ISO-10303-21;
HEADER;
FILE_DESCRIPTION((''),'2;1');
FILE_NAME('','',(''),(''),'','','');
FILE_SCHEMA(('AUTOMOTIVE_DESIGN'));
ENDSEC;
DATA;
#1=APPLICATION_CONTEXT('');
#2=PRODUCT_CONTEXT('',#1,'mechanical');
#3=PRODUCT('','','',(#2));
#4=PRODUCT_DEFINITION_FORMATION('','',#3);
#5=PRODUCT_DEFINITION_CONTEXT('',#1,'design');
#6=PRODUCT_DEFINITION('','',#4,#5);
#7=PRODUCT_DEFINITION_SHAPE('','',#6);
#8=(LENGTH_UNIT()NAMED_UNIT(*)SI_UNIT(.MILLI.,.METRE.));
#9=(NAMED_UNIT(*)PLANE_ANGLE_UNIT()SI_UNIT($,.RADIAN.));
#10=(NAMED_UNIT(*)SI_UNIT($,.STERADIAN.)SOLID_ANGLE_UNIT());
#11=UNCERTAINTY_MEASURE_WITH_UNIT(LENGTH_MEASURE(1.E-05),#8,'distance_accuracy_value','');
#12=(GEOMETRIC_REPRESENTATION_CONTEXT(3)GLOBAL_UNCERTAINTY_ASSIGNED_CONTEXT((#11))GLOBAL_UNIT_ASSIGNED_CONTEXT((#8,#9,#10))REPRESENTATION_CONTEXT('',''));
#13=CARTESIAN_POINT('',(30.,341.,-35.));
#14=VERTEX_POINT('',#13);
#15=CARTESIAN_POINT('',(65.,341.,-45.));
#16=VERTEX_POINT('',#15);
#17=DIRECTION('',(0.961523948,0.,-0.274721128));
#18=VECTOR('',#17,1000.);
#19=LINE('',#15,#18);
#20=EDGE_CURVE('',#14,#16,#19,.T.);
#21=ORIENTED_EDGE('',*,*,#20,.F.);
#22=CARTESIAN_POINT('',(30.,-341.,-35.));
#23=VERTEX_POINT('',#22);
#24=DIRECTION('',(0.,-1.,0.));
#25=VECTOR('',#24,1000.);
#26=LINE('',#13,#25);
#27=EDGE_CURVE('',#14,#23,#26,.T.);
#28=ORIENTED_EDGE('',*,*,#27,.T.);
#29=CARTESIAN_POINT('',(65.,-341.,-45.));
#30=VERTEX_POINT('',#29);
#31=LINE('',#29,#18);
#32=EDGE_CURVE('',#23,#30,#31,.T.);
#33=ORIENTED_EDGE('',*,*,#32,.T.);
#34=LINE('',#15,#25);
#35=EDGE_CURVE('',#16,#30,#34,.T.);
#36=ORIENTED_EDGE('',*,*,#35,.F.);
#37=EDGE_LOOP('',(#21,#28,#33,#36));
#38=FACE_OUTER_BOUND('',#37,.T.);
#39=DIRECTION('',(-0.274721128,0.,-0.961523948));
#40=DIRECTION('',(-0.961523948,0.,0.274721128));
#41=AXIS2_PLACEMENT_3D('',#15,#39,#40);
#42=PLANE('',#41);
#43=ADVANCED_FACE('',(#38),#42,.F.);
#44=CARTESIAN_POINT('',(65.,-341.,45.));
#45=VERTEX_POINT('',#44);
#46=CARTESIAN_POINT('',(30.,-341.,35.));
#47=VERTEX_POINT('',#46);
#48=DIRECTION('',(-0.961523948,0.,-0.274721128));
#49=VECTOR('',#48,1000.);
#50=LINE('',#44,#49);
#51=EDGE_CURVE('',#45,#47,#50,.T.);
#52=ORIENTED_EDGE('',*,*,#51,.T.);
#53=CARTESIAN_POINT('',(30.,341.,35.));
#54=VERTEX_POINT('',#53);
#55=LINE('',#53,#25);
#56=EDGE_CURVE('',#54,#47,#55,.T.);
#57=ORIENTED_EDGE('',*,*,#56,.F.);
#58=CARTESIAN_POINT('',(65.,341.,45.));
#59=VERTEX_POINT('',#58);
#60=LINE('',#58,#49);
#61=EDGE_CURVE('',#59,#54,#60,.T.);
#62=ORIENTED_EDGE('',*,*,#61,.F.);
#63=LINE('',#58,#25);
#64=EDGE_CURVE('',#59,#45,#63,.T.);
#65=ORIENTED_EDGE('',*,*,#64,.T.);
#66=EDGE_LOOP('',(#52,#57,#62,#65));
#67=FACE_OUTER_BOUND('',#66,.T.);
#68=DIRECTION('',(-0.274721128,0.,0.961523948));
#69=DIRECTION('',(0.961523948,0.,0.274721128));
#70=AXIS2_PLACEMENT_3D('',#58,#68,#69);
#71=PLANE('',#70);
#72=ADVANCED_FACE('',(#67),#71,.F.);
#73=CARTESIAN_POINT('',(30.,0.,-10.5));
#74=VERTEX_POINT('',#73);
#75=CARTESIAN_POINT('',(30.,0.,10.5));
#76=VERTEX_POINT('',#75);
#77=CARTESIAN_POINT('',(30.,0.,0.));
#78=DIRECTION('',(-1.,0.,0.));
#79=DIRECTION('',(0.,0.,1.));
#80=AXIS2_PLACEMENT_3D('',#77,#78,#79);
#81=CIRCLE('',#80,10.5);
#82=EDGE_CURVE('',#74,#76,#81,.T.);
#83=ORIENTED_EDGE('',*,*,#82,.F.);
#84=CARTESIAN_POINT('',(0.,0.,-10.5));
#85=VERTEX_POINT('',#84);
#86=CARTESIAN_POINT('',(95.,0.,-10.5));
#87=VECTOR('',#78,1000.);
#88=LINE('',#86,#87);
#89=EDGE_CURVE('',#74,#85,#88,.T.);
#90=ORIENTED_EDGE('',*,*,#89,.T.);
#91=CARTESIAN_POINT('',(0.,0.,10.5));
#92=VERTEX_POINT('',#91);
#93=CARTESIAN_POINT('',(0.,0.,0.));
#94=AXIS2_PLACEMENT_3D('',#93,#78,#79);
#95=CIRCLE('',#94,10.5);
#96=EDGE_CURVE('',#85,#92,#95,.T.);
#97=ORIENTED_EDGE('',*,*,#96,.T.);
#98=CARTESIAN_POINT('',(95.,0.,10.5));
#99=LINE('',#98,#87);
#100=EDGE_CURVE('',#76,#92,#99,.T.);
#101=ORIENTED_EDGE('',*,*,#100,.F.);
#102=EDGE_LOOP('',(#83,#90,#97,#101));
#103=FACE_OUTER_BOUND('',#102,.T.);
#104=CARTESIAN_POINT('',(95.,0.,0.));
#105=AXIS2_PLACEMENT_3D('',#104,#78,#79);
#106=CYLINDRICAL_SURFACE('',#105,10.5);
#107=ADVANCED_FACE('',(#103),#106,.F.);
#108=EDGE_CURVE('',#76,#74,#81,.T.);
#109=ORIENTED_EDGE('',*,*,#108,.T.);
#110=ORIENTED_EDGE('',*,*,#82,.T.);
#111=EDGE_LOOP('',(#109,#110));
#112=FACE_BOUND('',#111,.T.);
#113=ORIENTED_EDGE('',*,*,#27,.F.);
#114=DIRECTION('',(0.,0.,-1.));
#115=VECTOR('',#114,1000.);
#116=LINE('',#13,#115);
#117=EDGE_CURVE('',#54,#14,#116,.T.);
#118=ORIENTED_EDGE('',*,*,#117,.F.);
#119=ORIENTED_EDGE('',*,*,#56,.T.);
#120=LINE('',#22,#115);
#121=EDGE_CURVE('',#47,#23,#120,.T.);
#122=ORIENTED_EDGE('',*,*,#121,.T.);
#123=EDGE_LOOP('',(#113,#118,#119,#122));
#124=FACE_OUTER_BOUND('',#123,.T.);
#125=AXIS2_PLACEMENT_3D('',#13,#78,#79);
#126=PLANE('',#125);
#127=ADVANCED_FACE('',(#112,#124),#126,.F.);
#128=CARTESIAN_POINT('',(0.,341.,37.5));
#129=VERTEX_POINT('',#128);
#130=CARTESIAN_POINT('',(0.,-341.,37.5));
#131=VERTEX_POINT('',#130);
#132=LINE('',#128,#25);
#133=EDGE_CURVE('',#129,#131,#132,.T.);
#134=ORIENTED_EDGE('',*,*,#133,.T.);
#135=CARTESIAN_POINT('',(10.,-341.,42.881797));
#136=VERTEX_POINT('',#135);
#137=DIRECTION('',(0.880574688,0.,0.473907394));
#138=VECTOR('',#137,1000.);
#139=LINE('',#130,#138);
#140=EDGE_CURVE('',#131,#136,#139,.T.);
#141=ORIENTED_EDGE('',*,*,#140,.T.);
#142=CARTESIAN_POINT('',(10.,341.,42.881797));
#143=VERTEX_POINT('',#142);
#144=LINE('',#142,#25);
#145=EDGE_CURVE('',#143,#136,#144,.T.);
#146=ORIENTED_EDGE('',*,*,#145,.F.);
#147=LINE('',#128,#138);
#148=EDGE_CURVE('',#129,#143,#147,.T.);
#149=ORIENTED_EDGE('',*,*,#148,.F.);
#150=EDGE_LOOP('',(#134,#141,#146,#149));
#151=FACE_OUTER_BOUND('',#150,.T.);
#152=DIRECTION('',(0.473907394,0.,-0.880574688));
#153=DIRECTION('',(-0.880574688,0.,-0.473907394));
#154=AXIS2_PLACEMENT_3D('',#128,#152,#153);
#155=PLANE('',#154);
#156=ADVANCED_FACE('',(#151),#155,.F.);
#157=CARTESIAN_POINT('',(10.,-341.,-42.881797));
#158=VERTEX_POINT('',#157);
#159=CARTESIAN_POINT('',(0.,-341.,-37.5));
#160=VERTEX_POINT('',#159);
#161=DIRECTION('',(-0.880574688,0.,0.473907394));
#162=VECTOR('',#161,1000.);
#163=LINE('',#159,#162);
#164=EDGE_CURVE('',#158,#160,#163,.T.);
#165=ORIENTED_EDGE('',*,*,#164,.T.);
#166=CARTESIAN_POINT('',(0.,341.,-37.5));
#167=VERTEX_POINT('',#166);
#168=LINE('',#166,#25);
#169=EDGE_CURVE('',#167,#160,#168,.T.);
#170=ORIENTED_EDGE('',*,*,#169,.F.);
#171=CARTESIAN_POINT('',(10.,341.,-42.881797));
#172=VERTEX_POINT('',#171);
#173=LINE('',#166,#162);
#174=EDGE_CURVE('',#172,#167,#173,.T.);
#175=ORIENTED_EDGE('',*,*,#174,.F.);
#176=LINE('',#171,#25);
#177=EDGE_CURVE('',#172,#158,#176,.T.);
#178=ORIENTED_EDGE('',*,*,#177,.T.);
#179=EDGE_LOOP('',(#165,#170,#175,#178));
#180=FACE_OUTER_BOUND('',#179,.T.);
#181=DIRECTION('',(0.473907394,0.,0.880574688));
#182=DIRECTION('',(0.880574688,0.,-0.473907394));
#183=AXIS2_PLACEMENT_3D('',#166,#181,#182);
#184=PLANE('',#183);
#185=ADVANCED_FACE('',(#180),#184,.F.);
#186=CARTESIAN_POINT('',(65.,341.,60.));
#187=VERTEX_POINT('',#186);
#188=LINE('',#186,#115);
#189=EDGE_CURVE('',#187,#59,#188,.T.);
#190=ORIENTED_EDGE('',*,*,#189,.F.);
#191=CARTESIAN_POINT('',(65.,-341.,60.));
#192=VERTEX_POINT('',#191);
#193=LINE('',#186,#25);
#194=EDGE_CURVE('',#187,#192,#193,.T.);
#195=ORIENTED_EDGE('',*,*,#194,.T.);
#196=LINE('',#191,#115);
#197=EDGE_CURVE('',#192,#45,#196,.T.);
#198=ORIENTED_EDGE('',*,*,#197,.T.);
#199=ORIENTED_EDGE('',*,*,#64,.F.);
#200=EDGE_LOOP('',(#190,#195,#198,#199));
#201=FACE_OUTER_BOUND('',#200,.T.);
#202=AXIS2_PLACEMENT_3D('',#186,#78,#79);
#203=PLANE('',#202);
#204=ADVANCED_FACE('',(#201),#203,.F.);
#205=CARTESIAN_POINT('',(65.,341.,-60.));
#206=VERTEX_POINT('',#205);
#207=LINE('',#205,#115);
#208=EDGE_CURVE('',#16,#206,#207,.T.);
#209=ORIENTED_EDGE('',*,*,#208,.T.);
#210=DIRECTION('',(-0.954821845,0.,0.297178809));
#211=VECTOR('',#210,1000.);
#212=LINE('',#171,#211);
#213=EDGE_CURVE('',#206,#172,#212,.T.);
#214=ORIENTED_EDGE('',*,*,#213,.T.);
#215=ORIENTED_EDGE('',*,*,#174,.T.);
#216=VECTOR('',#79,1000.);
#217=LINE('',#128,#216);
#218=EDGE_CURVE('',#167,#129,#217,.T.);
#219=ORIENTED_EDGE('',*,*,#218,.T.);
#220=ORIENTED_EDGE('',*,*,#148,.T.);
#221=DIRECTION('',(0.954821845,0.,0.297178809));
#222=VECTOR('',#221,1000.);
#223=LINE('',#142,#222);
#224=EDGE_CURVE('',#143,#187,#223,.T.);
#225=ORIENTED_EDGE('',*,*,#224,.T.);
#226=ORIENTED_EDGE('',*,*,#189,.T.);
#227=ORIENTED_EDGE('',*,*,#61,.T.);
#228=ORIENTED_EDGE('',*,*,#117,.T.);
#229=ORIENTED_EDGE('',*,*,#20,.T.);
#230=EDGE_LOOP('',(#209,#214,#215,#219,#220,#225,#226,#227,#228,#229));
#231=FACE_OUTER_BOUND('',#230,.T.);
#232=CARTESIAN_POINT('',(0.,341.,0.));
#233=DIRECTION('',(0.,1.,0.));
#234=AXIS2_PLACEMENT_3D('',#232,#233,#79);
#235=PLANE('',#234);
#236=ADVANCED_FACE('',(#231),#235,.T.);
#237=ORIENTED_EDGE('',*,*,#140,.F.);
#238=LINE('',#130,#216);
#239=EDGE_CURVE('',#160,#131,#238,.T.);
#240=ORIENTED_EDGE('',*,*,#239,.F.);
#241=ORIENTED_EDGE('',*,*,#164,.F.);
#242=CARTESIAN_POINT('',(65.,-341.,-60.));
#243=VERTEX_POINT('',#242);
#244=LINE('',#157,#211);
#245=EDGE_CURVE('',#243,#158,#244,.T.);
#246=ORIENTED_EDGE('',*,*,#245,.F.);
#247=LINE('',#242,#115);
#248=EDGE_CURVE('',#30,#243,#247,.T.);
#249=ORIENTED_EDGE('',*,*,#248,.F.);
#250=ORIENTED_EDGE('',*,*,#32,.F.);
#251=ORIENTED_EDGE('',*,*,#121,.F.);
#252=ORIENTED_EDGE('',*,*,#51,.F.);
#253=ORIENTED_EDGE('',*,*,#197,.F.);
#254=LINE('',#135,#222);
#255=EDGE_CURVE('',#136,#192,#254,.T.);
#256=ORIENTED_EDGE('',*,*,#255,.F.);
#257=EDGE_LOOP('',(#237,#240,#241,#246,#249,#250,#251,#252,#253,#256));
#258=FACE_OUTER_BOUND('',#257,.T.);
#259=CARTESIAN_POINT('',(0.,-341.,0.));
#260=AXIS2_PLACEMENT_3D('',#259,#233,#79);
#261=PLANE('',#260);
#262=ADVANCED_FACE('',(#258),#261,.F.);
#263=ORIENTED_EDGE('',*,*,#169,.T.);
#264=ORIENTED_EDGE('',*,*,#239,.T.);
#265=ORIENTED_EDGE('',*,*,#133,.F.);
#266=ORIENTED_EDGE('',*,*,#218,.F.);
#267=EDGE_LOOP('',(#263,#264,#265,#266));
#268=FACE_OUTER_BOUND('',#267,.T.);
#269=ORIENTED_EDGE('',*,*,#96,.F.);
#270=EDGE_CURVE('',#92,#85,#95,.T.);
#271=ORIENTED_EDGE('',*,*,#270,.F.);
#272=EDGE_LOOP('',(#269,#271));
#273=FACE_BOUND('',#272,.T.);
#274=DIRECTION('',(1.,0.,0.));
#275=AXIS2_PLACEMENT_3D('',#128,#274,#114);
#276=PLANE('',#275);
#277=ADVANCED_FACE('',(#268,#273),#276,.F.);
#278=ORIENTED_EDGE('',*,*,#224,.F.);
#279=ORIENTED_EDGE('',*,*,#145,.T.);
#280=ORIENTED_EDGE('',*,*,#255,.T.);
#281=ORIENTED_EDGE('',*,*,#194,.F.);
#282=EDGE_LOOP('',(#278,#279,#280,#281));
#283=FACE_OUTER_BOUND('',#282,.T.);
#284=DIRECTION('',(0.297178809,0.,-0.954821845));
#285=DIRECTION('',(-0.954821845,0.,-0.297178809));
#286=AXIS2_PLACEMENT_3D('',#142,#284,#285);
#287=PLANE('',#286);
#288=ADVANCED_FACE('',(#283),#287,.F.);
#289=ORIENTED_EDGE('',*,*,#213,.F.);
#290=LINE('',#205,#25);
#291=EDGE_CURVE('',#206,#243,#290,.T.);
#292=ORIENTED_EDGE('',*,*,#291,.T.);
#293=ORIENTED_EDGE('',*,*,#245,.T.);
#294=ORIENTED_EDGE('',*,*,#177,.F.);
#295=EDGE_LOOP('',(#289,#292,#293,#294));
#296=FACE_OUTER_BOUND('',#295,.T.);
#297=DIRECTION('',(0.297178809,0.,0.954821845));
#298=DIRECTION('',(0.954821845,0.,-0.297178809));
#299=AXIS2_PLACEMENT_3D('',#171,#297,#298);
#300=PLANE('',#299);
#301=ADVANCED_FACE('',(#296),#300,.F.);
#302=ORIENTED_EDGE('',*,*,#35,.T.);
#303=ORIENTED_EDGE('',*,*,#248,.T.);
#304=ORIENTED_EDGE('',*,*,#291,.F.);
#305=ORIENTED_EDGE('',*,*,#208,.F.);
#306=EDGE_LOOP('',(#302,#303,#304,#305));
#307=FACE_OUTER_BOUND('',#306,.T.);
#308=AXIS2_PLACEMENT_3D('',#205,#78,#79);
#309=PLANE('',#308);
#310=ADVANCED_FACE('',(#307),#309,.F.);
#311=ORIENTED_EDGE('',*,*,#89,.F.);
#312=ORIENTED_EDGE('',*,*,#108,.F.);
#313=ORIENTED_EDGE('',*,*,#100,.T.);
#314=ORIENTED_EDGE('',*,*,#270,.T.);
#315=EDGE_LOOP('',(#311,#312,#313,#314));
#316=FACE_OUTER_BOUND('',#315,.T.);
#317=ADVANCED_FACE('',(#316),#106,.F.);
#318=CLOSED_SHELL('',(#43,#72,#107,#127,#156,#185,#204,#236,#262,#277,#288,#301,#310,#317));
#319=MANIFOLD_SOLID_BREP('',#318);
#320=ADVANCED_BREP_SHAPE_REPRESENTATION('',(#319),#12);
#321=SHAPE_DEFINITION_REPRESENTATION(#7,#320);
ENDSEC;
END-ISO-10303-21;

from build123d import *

# Parameters (mm, degrees)
BOSS_EXTRUDE1_DEPTH = 341
SKETCH2_R           = 10.5
CUT_EXTRUDE1_DEPTH  = 95


with BuildPart() as part:
    # Sketch1 → Boss-Extrude1 (new, symmetric)
    with BuildSketch(Plane(origin=(0, 0, 0), x_dir=(1, 0, 0), z_dir=(0, 1, 0))):
        Polygon((0, -37.5), (0, 37.5), (10, 42.881796684), (65, 60), (65, 45), (30, 35), (30, -35), (65, -45), (65, -60), (10, -42.881796684), align=None)
    extrude(amount=BOSS_EXTRUDE1_DEPTH, both=True)

    # Sketch2 → Cut-Extrude1 (cut)
    with BuildSketch(Plane.ZY):
        Circle(SKETCH2_R)
    extrude(amount=-CUT_EXTRUDE1_DEPTH, mode=Mode.SUBTRACT)


solid = part.part
